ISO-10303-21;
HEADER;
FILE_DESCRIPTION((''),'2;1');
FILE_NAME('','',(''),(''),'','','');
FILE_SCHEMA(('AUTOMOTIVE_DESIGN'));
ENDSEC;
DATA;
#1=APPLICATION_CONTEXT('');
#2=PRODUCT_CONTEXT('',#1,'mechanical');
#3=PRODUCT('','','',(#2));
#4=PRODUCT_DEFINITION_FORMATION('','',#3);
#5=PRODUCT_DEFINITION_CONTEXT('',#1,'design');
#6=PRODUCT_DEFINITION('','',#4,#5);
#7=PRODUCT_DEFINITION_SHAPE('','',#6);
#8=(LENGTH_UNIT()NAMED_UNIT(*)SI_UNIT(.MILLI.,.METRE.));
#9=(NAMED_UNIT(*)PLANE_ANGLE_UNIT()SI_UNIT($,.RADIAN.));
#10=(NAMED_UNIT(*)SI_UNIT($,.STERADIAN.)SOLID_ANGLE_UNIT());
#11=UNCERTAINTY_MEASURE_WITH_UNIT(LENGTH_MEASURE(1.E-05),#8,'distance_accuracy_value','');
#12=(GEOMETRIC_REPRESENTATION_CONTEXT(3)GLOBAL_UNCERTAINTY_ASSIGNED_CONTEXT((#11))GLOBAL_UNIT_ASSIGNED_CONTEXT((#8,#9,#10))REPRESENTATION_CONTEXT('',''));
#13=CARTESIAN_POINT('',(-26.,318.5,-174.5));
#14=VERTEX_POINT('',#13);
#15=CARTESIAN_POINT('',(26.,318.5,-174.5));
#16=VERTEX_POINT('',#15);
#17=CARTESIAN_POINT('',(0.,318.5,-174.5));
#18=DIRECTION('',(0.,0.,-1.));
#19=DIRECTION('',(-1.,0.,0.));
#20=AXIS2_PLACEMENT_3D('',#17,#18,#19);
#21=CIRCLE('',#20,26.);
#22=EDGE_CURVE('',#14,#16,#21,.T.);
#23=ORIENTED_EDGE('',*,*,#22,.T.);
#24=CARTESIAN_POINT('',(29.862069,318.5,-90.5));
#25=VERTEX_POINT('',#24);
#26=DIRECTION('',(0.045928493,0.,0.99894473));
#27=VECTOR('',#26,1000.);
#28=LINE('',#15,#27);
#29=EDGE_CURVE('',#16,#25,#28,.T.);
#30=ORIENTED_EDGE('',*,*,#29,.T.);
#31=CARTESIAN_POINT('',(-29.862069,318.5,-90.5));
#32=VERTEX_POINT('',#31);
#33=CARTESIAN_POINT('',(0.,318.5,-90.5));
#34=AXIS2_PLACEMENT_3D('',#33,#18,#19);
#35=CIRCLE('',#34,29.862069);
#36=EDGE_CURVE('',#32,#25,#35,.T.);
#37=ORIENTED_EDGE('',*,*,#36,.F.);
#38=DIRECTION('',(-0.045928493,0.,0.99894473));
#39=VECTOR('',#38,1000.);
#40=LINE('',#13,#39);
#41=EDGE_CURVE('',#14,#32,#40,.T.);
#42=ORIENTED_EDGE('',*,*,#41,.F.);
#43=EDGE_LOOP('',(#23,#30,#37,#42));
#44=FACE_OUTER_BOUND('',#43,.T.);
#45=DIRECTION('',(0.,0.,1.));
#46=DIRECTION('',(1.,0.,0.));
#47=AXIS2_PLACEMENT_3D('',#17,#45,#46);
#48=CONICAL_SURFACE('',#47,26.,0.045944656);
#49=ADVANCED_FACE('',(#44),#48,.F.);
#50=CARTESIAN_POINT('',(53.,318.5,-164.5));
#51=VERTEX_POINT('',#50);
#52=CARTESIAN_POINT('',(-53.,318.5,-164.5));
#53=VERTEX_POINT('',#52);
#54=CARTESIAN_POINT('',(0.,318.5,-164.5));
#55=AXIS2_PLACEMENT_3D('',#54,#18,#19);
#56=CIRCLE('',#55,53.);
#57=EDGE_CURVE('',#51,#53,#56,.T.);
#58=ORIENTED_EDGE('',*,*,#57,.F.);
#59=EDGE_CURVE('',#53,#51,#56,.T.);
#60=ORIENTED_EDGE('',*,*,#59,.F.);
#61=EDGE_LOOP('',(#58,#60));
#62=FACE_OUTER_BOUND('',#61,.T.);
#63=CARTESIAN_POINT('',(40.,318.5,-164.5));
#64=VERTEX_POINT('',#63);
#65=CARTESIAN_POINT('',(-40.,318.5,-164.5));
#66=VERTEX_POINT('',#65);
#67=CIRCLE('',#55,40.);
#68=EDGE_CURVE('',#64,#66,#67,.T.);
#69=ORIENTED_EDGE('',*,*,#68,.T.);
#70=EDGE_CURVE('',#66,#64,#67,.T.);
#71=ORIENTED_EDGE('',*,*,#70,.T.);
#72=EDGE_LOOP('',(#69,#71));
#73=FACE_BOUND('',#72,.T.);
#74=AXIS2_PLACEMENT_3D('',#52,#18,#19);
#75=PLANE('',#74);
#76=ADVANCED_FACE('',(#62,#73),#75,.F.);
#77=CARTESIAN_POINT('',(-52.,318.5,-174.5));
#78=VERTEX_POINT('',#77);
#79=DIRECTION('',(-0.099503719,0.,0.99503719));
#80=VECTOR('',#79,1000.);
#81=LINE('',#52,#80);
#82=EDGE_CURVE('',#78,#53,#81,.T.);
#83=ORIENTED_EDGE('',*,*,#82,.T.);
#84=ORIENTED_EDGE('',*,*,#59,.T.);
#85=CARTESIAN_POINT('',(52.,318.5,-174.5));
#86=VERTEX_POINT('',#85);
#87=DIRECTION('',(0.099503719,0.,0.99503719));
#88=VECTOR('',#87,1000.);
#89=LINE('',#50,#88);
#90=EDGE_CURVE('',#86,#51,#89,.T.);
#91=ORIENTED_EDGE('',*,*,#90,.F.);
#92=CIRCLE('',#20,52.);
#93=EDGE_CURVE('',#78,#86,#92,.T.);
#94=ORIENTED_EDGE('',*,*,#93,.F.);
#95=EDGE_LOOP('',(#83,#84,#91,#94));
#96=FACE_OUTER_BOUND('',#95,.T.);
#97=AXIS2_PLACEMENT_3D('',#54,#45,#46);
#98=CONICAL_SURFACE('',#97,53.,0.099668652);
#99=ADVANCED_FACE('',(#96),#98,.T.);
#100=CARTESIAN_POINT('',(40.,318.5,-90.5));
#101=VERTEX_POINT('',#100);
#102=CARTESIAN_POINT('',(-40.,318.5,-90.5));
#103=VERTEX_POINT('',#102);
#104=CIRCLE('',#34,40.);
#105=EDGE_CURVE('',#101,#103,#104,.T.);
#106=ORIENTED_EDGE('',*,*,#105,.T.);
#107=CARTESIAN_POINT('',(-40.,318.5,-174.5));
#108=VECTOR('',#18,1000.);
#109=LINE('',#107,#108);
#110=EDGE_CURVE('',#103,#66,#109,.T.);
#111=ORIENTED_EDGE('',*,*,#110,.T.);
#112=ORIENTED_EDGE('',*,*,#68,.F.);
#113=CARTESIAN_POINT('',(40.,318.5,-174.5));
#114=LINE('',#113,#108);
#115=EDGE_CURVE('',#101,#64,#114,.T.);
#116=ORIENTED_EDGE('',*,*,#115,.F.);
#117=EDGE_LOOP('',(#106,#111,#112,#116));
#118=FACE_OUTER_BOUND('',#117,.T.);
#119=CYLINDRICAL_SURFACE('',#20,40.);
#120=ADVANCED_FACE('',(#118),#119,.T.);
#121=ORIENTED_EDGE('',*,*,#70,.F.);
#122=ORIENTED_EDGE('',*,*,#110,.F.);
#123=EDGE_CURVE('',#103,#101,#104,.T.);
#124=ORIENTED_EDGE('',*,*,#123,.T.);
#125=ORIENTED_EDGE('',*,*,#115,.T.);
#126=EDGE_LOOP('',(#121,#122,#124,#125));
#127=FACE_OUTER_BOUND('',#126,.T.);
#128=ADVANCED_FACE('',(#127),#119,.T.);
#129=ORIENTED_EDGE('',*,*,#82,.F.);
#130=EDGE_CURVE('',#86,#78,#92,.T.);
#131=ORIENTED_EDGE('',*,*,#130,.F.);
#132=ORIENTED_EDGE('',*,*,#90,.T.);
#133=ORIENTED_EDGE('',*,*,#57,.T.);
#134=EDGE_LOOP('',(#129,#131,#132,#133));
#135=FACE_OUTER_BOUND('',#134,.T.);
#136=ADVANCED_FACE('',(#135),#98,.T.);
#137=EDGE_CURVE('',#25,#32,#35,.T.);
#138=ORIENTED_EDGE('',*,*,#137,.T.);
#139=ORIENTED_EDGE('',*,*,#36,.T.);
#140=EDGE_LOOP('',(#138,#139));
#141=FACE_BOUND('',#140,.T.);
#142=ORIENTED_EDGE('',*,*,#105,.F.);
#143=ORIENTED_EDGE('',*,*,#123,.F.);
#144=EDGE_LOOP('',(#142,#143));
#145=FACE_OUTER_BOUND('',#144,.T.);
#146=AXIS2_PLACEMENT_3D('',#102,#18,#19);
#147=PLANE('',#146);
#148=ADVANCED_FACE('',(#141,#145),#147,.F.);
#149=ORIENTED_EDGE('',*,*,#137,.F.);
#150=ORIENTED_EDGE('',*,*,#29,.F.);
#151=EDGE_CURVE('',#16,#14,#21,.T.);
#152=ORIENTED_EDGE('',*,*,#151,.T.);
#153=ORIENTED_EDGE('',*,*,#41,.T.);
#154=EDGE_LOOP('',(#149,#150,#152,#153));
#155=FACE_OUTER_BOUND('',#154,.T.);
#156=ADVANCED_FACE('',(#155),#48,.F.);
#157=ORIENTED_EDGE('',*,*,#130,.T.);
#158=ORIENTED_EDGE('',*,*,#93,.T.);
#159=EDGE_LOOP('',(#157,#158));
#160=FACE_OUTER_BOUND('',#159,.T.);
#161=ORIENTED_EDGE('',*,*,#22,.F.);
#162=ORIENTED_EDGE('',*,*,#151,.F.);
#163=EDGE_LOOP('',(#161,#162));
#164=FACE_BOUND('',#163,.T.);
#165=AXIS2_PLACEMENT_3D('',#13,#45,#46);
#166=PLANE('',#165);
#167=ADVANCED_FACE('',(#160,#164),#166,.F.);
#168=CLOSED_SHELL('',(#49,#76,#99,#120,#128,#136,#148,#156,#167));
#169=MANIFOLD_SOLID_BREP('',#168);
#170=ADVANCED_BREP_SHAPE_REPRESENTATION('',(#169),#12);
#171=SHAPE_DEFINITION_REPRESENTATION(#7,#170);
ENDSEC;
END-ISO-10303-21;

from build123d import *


with BuildPart() as part:
    # Sketch1 → Revolve1 (revolve)
    with BuildSketch(Plane(origin=(0, 318.5, 0), x_dir=(-1, 0, 0), z_dir=(0, -1, 0))):
        Polygon((40, 164.5), (40, 90.5), (29.862068966, 90.5), (26, 174.5), (52, 174.5), (53, 164.5), align=None)
    revolve(axis=Axis((0, 318.5, -174.5), (0, 0, 1)))


solid = part.part
